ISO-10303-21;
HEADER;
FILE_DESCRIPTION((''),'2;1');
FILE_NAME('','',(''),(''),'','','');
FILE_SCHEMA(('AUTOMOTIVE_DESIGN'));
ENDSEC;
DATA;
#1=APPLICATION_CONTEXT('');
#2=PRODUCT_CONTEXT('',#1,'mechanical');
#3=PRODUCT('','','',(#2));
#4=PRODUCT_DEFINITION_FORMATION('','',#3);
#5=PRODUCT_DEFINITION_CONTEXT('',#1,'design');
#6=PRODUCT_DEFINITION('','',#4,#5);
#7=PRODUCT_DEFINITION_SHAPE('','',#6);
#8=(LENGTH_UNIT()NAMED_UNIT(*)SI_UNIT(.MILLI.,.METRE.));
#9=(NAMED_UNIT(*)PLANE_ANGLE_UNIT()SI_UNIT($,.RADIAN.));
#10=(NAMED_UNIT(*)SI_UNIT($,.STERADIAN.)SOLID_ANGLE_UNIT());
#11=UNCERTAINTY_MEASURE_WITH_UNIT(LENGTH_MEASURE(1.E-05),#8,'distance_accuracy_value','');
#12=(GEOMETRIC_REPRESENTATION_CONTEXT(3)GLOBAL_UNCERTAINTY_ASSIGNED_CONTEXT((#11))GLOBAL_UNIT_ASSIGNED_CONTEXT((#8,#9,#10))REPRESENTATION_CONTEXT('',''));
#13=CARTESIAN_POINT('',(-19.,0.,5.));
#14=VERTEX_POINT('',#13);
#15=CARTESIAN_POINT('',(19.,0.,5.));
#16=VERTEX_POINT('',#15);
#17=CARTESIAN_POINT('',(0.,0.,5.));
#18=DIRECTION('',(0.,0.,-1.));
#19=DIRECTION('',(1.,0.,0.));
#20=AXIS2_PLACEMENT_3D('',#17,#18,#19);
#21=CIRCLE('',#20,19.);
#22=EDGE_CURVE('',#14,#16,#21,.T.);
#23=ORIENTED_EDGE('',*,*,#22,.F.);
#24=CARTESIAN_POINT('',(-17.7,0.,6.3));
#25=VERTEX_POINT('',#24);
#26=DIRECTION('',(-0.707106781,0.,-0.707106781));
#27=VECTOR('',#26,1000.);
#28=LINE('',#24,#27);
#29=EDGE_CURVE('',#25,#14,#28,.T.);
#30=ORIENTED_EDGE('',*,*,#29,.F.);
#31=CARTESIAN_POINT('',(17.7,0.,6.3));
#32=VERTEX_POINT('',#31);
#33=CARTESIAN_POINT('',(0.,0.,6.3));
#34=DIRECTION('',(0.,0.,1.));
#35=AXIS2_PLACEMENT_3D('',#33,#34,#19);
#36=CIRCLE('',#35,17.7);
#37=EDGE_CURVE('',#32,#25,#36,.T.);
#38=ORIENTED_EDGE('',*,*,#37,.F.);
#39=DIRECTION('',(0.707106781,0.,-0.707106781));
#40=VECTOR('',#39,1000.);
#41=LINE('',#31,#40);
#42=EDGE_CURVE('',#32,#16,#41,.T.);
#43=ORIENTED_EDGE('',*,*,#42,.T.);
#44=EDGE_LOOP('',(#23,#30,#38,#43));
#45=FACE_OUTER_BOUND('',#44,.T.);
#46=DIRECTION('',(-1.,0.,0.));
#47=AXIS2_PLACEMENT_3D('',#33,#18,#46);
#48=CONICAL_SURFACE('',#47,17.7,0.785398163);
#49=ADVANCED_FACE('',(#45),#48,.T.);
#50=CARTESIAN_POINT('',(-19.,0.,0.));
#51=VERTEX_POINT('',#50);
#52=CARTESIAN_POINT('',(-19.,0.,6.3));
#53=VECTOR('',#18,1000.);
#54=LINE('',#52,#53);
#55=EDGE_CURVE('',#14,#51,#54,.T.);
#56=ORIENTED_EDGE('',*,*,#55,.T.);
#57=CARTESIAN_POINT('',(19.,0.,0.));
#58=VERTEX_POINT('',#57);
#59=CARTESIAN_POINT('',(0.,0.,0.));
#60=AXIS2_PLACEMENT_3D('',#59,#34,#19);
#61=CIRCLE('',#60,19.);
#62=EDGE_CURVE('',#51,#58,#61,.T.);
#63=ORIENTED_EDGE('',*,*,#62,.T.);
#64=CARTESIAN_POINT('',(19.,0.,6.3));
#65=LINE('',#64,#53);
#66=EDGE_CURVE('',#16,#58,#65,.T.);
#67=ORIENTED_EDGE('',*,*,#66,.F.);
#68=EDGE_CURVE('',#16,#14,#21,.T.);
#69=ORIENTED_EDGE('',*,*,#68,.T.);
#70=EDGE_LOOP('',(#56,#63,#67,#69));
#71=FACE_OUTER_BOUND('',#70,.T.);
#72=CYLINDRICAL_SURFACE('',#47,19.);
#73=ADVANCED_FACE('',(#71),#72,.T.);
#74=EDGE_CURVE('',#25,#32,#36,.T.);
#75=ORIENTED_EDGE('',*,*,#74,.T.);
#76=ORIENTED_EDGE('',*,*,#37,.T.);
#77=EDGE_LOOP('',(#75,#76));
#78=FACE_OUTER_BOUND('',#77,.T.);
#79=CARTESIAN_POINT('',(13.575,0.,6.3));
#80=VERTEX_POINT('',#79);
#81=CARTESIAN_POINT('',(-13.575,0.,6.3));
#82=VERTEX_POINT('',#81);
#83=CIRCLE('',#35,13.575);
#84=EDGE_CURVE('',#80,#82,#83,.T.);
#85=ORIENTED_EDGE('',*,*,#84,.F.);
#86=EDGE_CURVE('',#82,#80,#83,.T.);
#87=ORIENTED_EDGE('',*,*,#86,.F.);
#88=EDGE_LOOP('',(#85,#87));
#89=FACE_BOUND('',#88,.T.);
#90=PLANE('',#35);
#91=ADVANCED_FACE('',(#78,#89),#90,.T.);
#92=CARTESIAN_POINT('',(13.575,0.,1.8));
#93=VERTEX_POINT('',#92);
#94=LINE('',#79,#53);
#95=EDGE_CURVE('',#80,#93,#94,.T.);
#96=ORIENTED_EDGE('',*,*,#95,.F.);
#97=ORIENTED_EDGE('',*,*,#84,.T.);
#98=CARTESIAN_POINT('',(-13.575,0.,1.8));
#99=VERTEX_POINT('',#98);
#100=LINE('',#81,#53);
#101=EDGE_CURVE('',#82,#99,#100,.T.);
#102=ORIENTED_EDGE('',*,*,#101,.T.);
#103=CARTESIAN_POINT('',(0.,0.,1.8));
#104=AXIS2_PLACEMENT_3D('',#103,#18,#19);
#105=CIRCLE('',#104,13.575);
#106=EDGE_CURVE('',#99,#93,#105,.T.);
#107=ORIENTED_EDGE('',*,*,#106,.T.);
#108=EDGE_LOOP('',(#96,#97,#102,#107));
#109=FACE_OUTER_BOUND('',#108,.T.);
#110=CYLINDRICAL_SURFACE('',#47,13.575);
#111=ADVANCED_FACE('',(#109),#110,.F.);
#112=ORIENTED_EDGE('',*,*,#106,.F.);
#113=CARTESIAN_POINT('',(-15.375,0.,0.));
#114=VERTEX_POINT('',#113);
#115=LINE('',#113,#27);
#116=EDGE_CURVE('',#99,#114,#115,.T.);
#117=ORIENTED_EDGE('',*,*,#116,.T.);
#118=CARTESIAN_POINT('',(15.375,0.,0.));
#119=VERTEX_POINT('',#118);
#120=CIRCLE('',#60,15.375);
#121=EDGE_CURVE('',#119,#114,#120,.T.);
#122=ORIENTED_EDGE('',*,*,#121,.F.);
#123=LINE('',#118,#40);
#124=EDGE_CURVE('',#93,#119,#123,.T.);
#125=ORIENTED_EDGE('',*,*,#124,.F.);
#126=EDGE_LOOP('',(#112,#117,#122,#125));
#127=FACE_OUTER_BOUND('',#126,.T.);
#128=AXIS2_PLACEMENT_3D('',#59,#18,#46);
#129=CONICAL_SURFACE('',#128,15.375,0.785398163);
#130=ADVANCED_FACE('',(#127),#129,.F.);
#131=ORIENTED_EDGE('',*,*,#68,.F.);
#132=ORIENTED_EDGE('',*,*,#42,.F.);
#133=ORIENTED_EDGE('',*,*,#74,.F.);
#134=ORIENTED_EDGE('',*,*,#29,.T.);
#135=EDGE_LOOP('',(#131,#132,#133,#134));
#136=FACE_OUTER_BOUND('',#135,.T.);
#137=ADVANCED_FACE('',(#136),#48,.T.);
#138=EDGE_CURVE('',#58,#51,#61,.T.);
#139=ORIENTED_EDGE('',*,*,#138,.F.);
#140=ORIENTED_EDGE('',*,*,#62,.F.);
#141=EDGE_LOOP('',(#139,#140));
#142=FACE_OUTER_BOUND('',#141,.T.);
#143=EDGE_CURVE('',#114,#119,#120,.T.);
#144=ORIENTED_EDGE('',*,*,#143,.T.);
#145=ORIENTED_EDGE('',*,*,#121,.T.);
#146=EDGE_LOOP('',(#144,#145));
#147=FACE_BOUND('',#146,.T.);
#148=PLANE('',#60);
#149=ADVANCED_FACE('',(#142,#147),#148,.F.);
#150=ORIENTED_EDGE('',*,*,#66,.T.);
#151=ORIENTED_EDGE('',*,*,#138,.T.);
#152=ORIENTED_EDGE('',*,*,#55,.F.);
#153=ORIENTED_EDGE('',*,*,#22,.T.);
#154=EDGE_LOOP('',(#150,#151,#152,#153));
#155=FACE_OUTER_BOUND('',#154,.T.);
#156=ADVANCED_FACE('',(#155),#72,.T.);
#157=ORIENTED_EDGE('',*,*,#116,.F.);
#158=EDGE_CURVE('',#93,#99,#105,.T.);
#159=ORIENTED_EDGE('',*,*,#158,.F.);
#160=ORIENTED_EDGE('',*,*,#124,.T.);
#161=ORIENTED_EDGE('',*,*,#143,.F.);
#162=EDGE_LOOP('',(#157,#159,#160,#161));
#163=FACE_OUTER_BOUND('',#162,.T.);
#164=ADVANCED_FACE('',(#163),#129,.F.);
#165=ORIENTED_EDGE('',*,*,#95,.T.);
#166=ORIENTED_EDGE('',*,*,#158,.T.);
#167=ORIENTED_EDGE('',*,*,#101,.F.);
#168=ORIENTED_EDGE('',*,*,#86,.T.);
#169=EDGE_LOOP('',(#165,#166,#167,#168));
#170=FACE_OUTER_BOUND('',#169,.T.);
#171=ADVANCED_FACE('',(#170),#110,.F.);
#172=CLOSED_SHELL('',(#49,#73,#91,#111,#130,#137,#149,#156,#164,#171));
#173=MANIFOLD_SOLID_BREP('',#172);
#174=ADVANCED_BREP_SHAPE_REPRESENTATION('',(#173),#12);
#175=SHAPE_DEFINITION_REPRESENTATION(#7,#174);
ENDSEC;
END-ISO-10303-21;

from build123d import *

# Parameters (mm, degrees)
SKETCH_1_R      = 19
SKETCH_1_R_2    = 13.575
EXTRUDE_1_DEPTH = 6.3
CHAMFER_1_SIZE  = 1.3
CHAMFER_2_SIZE  = 1.8


with BuildPart() as part:
    # 草图1 → 凸台-拉伸1 (new body)
    with BuildSketch(Plane.XY):
        Circle(SKETCH_1_R)
        Circle(SKETCH_1_R_2, mode=Mode.SUBTRACT)
    extrude(amount=EXTRUDE_1_DEPTH)

    # 倒角1
    chamfer_1_edges = [part.edges().sort_by_distance(p)[0] for p in [
        (-19, 0, 6.3),
    ]]
    chamfer(chamfer_1_edges, length=CHAMFER_1_SIZE)

    # 倒角2
    chamfer_2_edges = [part.edges().sort_by_distance(p)[0] for p in [
        (-13.575, 0, 0),
    ]]
    chamfer(chamfer_2_edges, length=CHAMFER_2_SIZE)


solid = part.part
